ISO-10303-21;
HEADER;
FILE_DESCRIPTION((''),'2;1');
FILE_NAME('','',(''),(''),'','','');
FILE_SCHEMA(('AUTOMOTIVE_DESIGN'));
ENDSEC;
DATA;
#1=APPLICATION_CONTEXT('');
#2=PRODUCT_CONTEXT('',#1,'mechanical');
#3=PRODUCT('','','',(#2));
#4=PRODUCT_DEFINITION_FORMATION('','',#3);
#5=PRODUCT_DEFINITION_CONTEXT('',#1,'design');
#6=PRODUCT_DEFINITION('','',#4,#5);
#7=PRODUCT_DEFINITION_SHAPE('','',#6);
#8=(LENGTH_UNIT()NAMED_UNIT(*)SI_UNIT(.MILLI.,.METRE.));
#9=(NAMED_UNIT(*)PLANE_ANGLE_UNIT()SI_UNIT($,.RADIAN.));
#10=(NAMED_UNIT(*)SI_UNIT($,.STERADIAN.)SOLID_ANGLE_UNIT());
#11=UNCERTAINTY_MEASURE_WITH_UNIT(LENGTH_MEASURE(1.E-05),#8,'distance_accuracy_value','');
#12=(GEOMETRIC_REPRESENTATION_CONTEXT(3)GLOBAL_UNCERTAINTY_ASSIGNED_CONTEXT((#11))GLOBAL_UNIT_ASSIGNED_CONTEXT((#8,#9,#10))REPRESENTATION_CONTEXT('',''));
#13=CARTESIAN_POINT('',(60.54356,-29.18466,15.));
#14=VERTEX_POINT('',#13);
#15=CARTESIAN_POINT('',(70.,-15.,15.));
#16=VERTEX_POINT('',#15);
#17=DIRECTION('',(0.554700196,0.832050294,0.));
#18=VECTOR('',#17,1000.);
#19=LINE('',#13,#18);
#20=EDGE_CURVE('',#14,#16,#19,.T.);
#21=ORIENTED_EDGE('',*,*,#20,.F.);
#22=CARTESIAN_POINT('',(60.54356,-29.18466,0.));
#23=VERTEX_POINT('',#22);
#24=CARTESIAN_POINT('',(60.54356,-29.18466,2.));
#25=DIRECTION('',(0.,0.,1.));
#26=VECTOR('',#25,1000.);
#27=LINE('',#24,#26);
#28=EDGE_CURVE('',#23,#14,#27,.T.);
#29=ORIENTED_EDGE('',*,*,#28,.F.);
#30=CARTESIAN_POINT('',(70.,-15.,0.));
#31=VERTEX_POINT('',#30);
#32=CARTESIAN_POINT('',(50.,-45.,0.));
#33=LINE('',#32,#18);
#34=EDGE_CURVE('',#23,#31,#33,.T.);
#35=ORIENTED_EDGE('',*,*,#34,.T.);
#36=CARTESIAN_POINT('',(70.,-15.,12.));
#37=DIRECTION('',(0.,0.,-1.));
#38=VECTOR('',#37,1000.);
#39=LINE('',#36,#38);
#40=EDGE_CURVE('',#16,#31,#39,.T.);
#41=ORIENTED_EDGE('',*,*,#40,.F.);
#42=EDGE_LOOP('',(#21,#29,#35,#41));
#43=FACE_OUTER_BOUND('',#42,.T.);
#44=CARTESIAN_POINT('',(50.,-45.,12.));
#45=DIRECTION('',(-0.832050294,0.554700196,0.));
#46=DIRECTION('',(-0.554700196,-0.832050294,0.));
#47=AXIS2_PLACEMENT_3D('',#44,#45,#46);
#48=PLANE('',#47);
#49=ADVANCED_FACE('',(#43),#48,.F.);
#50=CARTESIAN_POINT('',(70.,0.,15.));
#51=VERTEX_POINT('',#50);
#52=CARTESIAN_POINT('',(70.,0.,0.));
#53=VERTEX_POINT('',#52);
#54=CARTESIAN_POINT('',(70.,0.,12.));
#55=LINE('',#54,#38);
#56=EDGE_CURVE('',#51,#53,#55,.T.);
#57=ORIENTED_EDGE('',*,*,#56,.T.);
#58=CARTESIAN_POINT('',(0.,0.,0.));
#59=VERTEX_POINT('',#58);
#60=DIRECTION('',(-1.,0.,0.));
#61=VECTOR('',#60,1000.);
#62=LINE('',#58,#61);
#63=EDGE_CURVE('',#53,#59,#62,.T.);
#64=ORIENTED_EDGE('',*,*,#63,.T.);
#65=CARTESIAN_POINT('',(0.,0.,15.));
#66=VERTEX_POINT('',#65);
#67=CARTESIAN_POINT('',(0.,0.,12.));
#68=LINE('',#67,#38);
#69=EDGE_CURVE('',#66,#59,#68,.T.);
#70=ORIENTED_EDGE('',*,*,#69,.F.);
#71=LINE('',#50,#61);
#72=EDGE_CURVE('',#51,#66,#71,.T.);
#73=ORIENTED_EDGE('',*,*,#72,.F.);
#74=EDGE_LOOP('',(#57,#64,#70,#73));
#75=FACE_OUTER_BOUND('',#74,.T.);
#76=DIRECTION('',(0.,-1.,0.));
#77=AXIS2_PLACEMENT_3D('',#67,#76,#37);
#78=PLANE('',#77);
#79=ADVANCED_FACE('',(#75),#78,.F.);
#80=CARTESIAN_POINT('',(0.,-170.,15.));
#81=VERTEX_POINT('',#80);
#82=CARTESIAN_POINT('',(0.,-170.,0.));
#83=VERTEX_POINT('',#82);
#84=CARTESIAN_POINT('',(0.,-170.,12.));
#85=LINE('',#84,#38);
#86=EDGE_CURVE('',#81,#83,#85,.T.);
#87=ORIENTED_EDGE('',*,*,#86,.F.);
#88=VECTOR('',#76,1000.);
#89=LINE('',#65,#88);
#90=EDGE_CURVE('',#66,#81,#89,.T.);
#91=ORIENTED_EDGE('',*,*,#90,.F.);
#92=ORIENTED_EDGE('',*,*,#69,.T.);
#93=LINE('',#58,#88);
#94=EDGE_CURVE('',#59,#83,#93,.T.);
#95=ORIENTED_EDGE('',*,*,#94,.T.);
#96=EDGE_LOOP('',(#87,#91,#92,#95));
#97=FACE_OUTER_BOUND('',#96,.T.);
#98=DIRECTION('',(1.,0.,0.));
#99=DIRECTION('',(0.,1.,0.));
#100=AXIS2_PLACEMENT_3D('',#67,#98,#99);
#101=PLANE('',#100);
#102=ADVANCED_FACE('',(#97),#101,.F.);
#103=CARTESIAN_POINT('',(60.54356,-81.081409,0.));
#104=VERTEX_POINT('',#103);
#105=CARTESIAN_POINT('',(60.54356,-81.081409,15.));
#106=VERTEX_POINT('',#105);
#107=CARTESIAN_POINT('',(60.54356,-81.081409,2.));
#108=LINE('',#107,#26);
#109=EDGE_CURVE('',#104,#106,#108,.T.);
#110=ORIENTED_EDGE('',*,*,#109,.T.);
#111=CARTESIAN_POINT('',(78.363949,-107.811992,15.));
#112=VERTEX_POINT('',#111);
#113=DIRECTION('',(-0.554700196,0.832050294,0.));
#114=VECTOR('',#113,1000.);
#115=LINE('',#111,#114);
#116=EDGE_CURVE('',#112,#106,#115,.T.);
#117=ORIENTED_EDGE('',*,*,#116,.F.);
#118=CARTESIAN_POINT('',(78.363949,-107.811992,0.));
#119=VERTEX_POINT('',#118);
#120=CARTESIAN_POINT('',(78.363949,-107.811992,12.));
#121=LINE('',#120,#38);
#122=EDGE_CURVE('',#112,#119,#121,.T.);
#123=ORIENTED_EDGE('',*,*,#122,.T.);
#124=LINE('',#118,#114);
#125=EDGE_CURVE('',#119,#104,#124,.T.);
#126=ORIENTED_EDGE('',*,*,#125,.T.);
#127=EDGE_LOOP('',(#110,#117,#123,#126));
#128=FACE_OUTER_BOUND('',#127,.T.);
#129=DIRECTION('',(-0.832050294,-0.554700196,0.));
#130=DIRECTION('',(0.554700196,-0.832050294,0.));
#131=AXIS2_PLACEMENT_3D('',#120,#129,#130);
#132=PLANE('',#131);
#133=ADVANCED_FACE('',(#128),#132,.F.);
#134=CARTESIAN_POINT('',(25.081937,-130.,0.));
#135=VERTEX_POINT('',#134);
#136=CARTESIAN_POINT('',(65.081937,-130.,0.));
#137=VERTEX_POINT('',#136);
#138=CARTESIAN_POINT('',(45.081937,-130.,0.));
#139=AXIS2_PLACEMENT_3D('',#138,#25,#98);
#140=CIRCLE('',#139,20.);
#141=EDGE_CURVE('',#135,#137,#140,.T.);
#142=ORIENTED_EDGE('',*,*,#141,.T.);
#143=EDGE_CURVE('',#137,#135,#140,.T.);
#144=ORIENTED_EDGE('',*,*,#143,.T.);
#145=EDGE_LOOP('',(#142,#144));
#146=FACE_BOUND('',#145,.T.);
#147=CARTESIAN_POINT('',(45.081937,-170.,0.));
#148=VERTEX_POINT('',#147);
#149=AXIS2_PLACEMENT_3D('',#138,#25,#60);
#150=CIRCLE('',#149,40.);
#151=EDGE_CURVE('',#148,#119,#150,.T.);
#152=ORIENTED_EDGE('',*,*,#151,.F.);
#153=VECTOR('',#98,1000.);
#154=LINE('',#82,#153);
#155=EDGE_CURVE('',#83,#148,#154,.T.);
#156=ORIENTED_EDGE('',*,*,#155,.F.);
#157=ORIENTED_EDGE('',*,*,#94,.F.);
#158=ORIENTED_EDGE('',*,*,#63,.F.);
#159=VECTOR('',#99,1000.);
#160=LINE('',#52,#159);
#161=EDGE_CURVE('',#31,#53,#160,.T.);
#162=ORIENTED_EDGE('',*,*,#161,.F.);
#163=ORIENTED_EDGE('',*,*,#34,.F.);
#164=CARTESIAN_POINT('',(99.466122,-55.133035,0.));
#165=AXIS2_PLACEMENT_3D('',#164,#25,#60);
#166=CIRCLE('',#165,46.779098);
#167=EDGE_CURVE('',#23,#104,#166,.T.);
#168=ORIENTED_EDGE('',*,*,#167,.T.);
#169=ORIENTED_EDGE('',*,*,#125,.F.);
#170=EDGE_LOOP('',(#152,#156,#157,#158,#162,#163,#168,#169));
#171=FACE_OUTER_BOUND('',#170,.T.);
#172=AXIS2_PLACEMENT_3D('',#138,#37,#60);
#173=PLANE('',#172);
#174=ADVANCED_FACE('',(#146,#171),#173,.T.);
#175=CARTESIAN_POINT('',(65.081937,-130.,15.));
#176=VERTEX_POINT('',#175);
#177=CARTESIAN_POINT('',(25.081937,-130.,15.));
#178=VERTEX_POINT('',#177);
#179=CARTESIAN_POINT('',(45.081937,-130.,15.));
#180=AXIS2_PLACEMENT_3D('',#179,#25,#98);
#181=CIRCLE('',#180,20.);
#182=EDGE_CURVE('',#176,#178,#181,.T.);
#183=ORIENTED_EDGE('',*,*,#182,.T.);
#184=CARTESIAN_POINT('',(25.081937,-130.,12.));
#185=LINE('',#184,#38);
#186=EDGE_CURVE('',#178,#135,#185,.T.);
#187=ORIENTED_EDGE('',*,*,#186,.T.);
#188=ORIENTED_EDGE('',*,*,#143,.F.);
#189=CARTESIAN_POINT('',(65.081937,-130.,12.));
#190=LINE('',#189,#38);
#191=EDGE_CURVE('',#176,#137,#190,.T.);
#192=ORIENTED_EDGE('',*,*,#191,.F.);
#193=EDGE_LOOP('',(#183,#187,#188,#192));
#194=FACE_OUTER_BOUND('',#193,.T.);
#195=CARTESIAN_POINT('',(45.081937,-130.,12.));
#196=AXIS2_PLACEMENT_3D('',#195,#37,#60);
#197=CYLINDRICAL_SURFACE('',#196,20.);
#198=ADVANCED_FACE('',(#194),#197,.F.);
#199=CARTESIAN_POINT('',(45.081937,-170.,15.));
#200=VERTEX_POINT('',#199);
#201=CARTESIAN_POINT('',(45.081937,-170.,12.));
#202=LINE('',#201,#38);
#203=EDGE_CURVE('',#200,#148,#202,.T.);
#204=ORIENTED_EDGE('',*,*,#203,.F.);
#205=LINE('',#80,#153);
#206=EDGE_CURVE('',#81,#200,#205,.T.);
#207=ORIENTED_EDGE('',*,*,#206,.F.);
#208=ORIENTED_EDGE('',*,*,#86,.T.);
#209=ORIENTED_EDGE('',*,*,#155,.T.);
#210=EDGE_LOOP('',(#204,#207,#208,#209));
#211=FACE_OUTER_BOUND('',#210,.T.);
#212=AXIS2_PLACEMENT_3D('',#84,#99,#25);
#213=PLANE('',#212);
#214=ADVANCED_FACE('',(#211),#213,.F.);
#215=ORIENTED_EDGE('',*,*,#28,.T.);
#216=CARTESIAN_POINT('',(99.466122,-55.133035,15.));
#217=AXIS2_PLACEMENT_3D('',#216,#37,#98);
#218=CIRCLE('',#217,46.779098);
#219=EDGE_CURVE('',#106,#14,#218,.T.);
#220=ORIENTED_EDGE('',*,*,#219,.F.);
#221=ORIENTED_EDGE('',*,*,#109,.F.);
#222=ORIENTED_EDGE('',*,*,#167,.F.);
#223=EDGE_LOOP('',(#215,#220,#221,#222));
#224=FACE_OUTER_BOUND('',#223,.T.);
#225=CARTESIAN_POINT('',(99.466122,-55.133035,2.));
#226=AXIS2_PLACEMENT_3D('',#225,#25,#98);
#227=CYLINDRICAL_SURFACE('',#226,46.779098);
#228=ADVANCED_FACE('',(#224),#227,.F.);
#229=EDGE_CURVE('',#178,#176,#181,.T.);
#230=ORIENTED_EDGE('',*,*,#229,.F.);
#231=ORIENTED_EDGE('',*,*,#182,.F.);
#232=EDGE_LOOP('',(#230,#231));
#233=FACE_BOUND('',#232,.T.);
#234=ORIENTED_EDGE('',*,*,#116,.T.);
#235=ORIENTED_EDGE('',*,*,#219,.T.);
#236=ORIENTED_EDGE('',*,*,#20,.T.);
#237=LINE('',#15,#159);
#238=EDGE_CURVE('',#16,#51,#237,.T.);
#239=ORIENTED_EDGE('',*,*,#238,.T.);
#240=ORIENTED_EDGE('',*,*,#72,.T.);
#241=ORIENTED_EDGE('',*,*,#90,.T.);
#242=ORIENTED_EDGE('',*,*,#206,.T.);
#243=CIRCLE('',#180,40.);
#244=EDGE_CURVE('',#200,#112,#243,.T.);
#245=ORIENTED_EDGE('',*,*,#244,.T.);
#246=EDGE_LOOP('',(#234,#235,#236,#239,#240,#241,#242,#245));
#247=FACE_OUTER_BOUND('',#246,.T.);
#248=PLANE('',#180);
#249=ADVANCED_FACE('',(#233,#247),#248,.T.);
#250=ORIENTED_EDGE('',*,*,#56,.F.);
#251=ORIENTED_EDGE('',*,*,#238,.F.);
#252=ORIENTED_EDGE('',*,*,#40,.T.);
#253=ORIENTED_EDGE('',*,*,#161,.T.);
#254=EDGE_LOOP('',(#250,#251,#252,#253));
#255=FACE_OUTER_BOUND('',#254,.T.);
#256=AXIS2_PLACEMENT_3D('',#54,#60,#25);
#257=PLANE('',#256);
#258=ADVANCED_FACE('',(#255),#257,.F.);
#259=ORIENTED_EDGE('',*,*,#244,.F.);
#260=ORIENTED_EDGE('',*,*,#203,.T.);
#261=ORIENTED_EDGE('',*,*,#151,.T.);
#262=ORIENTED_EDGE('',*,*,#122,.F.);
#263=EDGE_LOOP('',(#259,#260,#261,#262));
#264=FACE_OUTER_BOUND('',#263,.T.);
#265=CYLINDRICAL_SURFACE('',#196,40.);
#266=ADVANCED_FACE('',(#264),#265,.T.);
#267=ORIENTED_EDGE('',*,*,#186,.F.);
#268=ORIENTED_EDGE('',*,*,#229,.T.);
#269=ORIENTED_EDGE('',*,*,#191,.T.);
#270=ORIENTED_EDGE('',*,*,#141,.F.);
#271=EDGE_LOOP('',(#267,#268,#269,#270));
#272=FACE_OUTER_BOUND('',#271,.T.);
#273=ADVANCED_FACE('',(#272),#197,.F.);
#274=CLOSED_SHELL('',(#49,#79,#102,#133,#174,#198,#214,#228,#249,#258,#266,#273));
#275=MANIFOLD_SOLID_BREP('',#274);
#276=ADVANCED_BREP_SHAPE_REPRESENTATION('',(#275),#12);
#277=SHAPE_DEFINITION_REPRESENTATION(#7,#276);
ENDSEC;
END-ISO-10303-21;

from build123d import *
from build123d.topology import SkipClean

# Parameters (mm, degrees)
SKETCH_1_R      = 20
EXTRUDE_1_DEPTH = 12
EXTRUDE_2_DEPTH = 10
EXTRUDE_3_DEPTH = 2
SKETCH_5_R      = 20
EXTRUDE_4_DEPTH = 3


with BuildPart() as part:
    # 草图1 → 凸台-拉伸1 (new body)
    with BuildSketch(Plane.XY):
        with BuildLine():
            Line((0, 0), (70, 0))
            Line((70, 0), (70, -15))
            Line((70, -15), (50, -45))
            Line((50, -45), (50, -65.266069056))
            Line((50, -65.266069056), (78.36394873, -107.811992151))
            ThreePointArc((78.36394873, -107.811992151), (80.348920907, -148.874317021), (45.081936956, -170))
            Line((45.081936956, -170), (0, -170))
            Line((0, -170), (0, 0))
        make_face()
        with Locations((45.081936956, -130)):
            Circle(SKETCH_1_R, mode=Mode.SUBTRACT)
    extrude(amount=EXTRUDE_1_DEPTH)

    # 草图3 → 凸台-拉伸2 (add)
    with BuildSketch(Plane.XY.offset(12)):
        with BuildLine():
            Line((50, -45), (50, -55.133034528))
            Line((50, -55.133034528), (52.687024396, -55.133034528))
            ThreePointArc((52.687024396, -55.133034528), (54.694220679, -41.57719354), (60.543560077, -29.184659884))
            Line((60.543560077, -29.184659884), (50, -45))
        make_face()
        with BuildLine():
            Line((52.687024396, -55.133034528), (50, -55.133034528))
            Line((50, -55.133034528), (50, -65.266069056))
            Line((50, -65.266069056), (60.543560077, -81.081409172))
            ThreePointArc((60.543560077, -81.081409172), (54.694220679, -68.688875516), (52.687024396, -55.133034528))
        make_face()
    extrude(amount=-EXTRUDE_2_DEPTH)

    # 草图4 → 凸台-拉伸3 (add)
    with BuildSketch(Plane(origin=(0, 0, 2), x_dir=(-1, 0, 0), z_dir=(0, 0, -1))):
        with BuildLine():
            Line((-60.543560077, -81.081409172), (-50, -65.266069056))
            Line((-50, -65.266069056), (-50, -45))
            Line((-50, -45), (-60.543560077, -29.184659884))
            ThreePointArc((-60.543560077, -29.184659884), (-52.687024396, -55.133034528), (-60.543560077, -81.081409172))
        make_face()
    extrude(amount=EXTRUDE_3_DEPTH)

    # 草图5 → 凸台-拉伸4 (add)
    with SkipClean():  # the faces are left unmerged after this step: merging them gives an invalid solid
        with BuildSketch(Plane.XY.offset(12)):
            with BuildLine():
                Line((0, 0), (0, -170))
                Line((0, -170), (45.081936956, -170))
                ThreePointArc((45.081936956, -170), (80.348920907, -148.874317021), (78.36394873, -107.811992151))
                Line((78.36394873, -107.811992151), (60.543560077, -81.081409172))
                ThreePointArc((60.543560077, -81.081409172), (52.687024396, -55.133034528), (60.543560077, -29.184659884))
                Line((60.543560077, -29.184659884), (70, -15))
                Line((70, -15), (70, 0))
                Line((70, 0), (0, 0))
            make_face()
            with Locations((45.081936956, -130)):
                Circle(SKETCH_5_R, mode=Mode.SUBTRACT)
        extrude(amount=EXTRUDE_4_DEPTH)


solid = part.part
